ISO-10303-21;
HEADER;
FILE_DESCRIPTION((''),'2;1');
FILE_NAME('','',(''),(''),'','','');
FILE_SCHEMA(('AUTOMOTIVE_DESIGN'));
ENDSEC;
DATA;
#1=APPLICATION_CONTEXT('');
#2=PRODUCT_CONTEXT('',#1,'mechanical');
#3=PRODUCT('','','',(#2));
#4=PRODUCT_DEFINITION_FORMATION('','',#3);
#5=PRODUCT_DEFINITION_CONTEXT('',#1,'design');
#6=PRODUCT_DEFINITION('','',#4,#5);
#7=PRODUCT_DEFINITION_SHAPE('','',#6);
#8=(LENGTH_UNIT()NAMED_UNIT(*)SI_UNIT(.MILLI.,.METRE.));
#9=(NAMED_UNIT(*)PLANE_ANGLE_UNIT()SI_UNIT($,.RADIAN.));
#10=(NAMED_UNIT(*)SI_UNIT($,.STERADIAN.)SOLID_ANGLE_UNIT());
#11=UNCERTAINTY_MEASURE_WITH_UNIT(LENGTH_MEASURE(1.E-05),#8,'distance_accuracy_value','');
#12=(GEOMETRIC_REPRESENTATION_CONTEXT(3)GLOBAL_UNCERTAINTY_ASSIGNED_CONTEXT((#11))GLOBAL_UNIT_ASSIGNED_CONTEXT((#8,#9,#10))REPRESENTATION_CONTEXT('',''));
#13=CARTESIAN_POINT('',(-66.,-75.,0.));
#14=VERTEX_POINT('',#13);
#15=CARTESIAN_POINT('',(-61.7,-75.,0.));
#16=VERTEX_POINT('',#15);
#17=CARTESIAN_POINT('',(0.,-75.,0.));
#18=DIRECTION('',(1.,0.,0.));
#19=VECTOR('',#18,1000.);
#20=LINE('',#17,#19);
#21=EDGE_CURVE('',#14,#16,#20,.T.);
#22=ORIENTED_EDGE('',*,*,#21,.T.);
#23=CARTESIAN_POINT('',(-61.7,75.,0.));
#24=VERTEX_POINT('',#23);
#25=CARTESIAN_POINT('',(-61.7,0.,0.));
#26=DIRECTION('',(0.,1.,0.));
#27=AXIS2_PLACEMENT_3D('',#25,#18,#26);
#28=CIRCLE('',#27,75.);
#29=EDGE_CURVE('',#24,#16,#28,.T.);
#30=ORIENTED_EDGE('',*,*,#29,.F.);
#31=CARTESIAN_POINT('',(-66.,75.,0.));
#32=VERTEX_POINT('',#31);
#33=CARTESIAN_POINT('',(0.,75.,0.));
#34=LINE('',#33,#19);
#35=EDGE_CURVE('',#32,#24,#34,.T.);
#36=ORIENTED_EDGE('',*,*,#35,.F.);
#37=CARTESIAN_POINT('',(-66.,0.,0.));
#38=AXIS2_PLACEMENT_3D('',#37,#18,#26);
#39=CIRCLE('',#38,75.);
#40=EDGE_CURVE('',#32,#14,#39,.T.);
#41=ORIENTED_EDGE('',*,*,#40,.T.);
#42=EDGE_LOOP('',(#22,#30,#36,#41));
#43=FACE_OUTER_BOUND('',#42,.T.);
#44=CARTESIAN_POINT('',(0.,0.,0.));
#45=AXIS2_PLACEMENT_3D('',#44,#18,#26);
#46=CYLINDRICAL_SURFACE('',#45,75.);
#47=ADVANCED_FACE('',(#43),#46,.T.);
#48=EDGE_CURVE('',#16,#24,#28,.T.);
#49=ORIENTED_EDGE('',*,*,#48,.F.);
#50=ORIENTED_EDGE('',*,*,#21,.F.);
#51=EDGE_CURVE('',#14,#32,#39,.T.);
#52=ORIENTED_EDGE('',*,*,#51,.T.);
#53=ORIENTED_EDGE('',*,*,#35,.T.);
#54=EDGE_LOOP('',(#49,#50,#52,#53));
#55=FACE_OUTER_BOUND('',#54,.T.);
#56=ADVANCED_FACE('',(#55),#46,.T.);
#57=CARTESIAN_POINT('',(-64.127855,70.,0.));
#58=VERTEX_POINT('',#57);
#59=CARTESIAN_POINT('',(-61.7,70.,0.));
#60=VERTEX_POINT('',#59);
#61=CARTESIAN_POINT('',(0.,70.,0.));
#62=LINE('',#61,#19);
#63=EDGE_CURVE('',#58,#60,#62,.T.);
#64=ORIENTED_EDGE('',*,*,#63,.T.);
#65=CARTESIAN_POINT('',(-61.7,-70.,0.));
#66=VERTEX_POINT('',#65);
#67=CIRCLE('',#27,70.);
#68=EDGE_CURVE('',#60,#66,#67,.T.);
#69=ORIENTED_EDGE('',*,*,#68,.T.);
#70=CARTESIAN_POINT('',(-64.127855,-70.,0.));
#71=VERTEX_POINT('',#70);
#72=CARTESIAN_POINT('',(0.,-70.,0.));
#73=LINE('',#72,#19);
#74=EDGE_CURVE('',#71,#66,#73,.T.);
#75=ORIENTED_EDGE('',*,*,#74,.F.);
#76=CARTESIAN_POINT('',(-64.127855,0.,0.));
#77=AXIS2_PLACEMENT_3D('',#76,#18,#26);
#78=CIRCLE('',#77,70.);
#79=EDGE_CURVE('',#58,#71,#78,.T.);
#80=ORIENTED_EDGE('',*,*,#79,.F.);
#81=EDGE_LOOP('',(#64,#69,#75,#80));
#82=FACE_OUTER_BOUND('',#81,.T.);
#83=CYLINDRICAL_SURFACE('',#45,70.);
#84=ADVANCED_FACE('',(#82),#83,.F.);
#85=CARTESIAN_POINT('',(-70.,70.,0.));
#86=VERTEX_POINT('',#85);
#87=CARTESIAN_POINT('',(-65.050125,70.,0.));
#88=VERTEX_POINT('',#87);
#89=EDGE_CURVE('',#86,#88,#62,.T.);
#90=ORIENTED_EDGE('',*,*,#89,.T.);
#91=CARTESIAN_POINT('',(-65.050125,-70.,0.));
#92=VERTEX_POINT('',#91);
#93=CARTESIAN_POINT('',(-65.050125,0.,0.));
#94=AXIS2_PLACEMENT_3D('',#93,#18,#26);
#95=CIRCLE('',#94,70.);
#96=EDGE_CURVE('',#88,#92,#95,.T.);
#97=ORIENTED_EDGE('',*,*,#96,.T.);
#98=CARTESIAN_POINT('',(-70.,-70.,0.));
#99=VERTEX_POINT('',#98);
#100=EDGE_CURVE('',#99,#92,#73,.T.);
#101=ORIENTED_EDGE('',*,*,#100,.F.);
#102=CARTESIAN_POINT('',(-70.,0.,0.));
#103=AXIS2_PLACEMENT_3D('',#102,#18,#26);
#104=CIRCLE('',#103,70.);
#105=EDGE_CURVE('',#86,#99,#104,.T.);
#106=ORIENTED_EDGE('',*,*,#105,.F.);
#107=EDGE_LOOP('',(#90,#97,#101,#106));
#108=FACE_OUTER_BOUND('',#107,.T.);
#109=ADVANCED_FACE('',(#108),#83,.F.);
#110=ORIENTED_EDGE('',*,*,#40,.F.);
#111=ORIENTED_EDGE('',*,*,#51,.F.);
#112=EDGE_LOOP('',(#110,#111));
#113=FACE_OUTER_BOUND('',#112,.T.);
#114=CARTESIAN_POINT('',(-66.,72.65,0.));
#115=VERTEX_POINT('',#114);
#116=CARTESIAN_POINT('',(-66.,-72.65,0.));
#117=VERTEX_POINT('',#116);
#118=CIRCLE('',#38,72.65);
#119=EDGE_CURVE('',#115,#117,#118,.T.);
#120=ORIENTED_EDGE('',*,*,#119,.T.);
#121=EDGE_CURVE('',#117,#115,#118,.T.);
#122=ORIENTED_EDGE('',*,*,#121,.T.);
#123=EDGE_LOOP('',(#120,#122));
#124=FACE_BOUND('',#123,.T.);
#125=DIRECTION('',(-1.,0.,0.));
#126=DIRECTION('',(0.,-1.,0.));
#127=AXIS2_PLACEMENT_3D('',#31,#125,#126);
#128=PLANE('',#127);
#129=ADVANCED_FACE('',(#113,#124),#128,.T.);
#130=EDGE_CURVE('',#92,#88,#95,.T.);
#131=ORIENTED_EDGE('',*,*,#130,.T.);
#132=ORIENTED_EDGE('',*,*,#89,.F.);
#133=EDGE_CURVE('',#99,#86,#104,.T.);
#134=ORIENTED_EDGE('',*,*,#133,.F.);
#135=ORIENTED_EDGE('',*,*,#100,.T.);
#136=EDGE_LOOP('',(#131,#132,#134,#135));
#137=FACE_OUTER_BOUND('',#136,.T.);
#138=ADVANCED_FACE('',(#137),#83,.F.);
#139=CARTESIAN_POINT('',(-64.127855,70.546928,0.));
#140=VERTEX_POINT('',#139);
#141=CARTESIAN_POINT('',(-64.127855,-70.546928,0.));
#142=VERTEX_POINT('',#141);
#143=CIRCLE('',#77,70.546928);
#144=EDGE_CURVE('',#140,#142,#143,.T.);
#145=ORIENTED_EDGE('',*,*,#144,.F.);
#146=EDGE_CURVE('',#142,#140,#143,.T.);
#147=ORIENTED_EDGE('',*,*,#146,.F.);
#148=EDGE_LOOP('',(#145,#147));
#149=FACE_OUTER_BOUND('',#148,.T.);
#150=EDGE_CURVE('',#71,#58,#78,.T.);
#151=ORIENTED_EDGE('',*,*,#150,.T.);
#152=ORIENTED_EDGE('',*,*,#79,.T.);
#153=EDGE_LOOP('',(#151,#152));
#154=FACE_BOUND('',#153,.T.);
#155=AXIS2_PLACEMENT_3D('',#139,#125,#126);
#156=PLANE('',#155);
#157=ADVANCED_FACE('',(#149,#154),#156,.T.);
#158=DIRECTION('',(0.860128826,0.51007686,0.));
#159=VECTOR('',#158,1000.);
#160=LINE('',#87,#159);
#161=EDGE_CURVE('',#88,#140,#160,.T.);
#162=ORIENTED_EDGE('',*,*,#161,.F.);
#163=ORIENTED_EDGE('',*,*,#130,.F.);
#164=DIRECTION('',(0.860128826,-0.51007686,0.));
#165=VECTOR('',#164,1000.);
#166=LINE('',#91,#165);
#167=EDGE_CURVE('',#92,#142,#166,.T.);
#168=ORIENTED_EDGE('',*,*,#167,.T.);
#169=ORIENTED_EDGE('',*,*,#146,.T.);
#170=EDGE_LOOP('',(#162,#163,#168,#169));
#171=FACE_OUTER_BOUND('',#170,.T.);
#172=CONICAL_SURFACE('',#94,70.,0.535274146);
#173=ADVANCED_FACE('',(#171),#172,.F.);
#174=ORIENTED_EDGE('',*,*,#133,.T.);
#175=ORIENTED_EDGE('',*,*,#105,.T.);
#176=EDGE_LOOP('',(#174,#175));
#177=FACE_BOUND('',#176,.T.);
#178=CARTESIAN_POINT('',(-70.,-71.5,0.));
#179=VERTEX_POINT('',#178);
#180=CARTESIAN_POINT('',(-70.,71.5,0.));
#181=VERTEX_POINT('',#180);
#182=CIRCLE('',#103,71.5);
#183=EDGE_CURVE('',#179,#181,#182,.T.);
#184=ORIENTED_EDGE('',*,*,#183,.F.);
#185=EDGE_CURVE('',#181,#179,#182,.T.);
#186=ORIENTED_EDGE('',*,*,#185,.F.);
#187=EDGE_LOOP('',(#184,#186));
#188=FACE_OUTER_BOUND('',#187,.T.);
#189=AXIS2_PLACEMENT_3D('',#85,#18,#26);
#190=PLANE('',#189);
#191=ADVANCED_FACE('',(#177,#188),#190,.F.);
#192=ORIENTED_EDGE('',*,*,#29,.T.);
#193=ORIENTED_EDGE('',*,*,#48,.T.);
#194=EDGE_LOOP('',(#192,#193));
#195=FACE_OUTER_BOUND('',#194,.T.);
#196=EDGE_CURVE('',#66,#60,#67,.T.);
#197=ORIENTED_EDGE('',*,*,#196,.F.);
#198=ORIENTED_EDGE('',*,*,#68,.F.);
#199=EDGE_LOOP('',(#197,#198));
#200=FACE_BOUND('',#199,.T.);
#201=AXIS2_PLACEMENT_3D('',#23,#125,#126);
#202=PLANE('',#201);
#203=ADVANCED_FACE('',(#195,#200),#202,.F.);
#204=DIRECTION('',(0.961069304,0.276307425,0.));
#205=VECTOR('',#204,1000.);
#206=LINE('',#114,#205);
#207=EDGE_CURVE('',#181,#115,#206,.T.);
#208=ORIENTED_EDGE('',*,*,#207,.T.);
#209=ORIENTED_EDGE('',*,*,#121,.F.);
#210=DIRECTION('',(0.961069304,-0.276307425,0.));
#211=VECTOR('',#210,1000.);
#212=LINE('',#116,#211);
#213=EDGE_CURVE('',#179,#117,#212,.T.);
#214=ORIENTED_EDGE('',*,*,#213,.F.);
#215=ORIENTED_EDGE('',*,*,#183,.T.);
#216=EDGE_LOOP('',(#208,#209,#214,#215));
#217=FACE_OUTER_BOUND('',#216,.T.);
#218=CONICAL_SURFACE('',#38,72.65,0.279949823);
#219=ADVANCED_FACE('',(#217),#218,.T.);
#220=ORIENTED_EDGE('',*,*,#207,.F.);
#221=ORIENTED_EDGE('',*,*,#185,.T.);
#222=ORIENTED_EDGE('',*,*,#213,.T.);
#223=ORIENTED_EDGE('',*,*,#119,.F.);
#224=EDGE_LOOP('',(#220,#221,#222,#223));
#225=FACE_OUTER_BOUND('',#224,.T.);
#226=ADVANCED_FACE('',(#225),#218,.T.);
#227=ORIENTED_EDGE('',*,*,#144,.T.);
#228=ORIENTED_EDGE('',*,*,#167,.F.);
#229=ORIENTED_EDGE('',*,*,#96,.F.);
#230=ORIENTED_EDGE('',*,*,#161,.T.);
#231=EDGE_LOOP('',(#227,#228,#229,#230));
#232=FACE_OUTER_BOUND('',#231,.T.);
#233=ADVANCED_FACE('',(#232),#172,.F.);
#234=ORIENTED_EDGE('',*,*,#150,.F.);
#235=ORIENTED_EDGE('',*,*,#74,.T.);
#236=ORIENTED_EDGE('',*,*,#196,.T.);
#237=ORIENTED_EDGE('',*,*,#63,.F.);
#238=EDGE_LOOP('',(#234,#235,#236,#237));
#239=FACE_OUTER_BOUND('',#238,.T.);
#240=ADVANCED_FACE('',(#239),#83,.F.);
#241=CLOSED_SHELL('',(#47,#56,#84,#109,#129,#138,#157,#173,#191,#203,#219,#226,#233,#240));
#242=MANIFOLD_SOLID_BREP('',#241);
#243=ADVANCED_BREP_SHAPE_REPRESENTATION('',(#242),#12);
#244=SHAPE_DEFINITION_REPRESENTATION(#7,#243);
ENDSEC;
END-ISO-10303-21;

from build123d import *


with BuildPart() as part:
    # Sketch1 → Revolve1 (revolve)
    with BuildSketch(Plane.XY):
        Polygon((-70, 70), (-70, 71.5), (-66, 72.65), (-66, 75), (-61.7, 75), (-61.7, 70), (-64.127855471, 70), (-64.127855471, 70.546927726), (-65.050124916, 70), align=None)
    revolve(axis=Axis((0, 0, 0), (-1, 0, 0)))


solid = part.part
